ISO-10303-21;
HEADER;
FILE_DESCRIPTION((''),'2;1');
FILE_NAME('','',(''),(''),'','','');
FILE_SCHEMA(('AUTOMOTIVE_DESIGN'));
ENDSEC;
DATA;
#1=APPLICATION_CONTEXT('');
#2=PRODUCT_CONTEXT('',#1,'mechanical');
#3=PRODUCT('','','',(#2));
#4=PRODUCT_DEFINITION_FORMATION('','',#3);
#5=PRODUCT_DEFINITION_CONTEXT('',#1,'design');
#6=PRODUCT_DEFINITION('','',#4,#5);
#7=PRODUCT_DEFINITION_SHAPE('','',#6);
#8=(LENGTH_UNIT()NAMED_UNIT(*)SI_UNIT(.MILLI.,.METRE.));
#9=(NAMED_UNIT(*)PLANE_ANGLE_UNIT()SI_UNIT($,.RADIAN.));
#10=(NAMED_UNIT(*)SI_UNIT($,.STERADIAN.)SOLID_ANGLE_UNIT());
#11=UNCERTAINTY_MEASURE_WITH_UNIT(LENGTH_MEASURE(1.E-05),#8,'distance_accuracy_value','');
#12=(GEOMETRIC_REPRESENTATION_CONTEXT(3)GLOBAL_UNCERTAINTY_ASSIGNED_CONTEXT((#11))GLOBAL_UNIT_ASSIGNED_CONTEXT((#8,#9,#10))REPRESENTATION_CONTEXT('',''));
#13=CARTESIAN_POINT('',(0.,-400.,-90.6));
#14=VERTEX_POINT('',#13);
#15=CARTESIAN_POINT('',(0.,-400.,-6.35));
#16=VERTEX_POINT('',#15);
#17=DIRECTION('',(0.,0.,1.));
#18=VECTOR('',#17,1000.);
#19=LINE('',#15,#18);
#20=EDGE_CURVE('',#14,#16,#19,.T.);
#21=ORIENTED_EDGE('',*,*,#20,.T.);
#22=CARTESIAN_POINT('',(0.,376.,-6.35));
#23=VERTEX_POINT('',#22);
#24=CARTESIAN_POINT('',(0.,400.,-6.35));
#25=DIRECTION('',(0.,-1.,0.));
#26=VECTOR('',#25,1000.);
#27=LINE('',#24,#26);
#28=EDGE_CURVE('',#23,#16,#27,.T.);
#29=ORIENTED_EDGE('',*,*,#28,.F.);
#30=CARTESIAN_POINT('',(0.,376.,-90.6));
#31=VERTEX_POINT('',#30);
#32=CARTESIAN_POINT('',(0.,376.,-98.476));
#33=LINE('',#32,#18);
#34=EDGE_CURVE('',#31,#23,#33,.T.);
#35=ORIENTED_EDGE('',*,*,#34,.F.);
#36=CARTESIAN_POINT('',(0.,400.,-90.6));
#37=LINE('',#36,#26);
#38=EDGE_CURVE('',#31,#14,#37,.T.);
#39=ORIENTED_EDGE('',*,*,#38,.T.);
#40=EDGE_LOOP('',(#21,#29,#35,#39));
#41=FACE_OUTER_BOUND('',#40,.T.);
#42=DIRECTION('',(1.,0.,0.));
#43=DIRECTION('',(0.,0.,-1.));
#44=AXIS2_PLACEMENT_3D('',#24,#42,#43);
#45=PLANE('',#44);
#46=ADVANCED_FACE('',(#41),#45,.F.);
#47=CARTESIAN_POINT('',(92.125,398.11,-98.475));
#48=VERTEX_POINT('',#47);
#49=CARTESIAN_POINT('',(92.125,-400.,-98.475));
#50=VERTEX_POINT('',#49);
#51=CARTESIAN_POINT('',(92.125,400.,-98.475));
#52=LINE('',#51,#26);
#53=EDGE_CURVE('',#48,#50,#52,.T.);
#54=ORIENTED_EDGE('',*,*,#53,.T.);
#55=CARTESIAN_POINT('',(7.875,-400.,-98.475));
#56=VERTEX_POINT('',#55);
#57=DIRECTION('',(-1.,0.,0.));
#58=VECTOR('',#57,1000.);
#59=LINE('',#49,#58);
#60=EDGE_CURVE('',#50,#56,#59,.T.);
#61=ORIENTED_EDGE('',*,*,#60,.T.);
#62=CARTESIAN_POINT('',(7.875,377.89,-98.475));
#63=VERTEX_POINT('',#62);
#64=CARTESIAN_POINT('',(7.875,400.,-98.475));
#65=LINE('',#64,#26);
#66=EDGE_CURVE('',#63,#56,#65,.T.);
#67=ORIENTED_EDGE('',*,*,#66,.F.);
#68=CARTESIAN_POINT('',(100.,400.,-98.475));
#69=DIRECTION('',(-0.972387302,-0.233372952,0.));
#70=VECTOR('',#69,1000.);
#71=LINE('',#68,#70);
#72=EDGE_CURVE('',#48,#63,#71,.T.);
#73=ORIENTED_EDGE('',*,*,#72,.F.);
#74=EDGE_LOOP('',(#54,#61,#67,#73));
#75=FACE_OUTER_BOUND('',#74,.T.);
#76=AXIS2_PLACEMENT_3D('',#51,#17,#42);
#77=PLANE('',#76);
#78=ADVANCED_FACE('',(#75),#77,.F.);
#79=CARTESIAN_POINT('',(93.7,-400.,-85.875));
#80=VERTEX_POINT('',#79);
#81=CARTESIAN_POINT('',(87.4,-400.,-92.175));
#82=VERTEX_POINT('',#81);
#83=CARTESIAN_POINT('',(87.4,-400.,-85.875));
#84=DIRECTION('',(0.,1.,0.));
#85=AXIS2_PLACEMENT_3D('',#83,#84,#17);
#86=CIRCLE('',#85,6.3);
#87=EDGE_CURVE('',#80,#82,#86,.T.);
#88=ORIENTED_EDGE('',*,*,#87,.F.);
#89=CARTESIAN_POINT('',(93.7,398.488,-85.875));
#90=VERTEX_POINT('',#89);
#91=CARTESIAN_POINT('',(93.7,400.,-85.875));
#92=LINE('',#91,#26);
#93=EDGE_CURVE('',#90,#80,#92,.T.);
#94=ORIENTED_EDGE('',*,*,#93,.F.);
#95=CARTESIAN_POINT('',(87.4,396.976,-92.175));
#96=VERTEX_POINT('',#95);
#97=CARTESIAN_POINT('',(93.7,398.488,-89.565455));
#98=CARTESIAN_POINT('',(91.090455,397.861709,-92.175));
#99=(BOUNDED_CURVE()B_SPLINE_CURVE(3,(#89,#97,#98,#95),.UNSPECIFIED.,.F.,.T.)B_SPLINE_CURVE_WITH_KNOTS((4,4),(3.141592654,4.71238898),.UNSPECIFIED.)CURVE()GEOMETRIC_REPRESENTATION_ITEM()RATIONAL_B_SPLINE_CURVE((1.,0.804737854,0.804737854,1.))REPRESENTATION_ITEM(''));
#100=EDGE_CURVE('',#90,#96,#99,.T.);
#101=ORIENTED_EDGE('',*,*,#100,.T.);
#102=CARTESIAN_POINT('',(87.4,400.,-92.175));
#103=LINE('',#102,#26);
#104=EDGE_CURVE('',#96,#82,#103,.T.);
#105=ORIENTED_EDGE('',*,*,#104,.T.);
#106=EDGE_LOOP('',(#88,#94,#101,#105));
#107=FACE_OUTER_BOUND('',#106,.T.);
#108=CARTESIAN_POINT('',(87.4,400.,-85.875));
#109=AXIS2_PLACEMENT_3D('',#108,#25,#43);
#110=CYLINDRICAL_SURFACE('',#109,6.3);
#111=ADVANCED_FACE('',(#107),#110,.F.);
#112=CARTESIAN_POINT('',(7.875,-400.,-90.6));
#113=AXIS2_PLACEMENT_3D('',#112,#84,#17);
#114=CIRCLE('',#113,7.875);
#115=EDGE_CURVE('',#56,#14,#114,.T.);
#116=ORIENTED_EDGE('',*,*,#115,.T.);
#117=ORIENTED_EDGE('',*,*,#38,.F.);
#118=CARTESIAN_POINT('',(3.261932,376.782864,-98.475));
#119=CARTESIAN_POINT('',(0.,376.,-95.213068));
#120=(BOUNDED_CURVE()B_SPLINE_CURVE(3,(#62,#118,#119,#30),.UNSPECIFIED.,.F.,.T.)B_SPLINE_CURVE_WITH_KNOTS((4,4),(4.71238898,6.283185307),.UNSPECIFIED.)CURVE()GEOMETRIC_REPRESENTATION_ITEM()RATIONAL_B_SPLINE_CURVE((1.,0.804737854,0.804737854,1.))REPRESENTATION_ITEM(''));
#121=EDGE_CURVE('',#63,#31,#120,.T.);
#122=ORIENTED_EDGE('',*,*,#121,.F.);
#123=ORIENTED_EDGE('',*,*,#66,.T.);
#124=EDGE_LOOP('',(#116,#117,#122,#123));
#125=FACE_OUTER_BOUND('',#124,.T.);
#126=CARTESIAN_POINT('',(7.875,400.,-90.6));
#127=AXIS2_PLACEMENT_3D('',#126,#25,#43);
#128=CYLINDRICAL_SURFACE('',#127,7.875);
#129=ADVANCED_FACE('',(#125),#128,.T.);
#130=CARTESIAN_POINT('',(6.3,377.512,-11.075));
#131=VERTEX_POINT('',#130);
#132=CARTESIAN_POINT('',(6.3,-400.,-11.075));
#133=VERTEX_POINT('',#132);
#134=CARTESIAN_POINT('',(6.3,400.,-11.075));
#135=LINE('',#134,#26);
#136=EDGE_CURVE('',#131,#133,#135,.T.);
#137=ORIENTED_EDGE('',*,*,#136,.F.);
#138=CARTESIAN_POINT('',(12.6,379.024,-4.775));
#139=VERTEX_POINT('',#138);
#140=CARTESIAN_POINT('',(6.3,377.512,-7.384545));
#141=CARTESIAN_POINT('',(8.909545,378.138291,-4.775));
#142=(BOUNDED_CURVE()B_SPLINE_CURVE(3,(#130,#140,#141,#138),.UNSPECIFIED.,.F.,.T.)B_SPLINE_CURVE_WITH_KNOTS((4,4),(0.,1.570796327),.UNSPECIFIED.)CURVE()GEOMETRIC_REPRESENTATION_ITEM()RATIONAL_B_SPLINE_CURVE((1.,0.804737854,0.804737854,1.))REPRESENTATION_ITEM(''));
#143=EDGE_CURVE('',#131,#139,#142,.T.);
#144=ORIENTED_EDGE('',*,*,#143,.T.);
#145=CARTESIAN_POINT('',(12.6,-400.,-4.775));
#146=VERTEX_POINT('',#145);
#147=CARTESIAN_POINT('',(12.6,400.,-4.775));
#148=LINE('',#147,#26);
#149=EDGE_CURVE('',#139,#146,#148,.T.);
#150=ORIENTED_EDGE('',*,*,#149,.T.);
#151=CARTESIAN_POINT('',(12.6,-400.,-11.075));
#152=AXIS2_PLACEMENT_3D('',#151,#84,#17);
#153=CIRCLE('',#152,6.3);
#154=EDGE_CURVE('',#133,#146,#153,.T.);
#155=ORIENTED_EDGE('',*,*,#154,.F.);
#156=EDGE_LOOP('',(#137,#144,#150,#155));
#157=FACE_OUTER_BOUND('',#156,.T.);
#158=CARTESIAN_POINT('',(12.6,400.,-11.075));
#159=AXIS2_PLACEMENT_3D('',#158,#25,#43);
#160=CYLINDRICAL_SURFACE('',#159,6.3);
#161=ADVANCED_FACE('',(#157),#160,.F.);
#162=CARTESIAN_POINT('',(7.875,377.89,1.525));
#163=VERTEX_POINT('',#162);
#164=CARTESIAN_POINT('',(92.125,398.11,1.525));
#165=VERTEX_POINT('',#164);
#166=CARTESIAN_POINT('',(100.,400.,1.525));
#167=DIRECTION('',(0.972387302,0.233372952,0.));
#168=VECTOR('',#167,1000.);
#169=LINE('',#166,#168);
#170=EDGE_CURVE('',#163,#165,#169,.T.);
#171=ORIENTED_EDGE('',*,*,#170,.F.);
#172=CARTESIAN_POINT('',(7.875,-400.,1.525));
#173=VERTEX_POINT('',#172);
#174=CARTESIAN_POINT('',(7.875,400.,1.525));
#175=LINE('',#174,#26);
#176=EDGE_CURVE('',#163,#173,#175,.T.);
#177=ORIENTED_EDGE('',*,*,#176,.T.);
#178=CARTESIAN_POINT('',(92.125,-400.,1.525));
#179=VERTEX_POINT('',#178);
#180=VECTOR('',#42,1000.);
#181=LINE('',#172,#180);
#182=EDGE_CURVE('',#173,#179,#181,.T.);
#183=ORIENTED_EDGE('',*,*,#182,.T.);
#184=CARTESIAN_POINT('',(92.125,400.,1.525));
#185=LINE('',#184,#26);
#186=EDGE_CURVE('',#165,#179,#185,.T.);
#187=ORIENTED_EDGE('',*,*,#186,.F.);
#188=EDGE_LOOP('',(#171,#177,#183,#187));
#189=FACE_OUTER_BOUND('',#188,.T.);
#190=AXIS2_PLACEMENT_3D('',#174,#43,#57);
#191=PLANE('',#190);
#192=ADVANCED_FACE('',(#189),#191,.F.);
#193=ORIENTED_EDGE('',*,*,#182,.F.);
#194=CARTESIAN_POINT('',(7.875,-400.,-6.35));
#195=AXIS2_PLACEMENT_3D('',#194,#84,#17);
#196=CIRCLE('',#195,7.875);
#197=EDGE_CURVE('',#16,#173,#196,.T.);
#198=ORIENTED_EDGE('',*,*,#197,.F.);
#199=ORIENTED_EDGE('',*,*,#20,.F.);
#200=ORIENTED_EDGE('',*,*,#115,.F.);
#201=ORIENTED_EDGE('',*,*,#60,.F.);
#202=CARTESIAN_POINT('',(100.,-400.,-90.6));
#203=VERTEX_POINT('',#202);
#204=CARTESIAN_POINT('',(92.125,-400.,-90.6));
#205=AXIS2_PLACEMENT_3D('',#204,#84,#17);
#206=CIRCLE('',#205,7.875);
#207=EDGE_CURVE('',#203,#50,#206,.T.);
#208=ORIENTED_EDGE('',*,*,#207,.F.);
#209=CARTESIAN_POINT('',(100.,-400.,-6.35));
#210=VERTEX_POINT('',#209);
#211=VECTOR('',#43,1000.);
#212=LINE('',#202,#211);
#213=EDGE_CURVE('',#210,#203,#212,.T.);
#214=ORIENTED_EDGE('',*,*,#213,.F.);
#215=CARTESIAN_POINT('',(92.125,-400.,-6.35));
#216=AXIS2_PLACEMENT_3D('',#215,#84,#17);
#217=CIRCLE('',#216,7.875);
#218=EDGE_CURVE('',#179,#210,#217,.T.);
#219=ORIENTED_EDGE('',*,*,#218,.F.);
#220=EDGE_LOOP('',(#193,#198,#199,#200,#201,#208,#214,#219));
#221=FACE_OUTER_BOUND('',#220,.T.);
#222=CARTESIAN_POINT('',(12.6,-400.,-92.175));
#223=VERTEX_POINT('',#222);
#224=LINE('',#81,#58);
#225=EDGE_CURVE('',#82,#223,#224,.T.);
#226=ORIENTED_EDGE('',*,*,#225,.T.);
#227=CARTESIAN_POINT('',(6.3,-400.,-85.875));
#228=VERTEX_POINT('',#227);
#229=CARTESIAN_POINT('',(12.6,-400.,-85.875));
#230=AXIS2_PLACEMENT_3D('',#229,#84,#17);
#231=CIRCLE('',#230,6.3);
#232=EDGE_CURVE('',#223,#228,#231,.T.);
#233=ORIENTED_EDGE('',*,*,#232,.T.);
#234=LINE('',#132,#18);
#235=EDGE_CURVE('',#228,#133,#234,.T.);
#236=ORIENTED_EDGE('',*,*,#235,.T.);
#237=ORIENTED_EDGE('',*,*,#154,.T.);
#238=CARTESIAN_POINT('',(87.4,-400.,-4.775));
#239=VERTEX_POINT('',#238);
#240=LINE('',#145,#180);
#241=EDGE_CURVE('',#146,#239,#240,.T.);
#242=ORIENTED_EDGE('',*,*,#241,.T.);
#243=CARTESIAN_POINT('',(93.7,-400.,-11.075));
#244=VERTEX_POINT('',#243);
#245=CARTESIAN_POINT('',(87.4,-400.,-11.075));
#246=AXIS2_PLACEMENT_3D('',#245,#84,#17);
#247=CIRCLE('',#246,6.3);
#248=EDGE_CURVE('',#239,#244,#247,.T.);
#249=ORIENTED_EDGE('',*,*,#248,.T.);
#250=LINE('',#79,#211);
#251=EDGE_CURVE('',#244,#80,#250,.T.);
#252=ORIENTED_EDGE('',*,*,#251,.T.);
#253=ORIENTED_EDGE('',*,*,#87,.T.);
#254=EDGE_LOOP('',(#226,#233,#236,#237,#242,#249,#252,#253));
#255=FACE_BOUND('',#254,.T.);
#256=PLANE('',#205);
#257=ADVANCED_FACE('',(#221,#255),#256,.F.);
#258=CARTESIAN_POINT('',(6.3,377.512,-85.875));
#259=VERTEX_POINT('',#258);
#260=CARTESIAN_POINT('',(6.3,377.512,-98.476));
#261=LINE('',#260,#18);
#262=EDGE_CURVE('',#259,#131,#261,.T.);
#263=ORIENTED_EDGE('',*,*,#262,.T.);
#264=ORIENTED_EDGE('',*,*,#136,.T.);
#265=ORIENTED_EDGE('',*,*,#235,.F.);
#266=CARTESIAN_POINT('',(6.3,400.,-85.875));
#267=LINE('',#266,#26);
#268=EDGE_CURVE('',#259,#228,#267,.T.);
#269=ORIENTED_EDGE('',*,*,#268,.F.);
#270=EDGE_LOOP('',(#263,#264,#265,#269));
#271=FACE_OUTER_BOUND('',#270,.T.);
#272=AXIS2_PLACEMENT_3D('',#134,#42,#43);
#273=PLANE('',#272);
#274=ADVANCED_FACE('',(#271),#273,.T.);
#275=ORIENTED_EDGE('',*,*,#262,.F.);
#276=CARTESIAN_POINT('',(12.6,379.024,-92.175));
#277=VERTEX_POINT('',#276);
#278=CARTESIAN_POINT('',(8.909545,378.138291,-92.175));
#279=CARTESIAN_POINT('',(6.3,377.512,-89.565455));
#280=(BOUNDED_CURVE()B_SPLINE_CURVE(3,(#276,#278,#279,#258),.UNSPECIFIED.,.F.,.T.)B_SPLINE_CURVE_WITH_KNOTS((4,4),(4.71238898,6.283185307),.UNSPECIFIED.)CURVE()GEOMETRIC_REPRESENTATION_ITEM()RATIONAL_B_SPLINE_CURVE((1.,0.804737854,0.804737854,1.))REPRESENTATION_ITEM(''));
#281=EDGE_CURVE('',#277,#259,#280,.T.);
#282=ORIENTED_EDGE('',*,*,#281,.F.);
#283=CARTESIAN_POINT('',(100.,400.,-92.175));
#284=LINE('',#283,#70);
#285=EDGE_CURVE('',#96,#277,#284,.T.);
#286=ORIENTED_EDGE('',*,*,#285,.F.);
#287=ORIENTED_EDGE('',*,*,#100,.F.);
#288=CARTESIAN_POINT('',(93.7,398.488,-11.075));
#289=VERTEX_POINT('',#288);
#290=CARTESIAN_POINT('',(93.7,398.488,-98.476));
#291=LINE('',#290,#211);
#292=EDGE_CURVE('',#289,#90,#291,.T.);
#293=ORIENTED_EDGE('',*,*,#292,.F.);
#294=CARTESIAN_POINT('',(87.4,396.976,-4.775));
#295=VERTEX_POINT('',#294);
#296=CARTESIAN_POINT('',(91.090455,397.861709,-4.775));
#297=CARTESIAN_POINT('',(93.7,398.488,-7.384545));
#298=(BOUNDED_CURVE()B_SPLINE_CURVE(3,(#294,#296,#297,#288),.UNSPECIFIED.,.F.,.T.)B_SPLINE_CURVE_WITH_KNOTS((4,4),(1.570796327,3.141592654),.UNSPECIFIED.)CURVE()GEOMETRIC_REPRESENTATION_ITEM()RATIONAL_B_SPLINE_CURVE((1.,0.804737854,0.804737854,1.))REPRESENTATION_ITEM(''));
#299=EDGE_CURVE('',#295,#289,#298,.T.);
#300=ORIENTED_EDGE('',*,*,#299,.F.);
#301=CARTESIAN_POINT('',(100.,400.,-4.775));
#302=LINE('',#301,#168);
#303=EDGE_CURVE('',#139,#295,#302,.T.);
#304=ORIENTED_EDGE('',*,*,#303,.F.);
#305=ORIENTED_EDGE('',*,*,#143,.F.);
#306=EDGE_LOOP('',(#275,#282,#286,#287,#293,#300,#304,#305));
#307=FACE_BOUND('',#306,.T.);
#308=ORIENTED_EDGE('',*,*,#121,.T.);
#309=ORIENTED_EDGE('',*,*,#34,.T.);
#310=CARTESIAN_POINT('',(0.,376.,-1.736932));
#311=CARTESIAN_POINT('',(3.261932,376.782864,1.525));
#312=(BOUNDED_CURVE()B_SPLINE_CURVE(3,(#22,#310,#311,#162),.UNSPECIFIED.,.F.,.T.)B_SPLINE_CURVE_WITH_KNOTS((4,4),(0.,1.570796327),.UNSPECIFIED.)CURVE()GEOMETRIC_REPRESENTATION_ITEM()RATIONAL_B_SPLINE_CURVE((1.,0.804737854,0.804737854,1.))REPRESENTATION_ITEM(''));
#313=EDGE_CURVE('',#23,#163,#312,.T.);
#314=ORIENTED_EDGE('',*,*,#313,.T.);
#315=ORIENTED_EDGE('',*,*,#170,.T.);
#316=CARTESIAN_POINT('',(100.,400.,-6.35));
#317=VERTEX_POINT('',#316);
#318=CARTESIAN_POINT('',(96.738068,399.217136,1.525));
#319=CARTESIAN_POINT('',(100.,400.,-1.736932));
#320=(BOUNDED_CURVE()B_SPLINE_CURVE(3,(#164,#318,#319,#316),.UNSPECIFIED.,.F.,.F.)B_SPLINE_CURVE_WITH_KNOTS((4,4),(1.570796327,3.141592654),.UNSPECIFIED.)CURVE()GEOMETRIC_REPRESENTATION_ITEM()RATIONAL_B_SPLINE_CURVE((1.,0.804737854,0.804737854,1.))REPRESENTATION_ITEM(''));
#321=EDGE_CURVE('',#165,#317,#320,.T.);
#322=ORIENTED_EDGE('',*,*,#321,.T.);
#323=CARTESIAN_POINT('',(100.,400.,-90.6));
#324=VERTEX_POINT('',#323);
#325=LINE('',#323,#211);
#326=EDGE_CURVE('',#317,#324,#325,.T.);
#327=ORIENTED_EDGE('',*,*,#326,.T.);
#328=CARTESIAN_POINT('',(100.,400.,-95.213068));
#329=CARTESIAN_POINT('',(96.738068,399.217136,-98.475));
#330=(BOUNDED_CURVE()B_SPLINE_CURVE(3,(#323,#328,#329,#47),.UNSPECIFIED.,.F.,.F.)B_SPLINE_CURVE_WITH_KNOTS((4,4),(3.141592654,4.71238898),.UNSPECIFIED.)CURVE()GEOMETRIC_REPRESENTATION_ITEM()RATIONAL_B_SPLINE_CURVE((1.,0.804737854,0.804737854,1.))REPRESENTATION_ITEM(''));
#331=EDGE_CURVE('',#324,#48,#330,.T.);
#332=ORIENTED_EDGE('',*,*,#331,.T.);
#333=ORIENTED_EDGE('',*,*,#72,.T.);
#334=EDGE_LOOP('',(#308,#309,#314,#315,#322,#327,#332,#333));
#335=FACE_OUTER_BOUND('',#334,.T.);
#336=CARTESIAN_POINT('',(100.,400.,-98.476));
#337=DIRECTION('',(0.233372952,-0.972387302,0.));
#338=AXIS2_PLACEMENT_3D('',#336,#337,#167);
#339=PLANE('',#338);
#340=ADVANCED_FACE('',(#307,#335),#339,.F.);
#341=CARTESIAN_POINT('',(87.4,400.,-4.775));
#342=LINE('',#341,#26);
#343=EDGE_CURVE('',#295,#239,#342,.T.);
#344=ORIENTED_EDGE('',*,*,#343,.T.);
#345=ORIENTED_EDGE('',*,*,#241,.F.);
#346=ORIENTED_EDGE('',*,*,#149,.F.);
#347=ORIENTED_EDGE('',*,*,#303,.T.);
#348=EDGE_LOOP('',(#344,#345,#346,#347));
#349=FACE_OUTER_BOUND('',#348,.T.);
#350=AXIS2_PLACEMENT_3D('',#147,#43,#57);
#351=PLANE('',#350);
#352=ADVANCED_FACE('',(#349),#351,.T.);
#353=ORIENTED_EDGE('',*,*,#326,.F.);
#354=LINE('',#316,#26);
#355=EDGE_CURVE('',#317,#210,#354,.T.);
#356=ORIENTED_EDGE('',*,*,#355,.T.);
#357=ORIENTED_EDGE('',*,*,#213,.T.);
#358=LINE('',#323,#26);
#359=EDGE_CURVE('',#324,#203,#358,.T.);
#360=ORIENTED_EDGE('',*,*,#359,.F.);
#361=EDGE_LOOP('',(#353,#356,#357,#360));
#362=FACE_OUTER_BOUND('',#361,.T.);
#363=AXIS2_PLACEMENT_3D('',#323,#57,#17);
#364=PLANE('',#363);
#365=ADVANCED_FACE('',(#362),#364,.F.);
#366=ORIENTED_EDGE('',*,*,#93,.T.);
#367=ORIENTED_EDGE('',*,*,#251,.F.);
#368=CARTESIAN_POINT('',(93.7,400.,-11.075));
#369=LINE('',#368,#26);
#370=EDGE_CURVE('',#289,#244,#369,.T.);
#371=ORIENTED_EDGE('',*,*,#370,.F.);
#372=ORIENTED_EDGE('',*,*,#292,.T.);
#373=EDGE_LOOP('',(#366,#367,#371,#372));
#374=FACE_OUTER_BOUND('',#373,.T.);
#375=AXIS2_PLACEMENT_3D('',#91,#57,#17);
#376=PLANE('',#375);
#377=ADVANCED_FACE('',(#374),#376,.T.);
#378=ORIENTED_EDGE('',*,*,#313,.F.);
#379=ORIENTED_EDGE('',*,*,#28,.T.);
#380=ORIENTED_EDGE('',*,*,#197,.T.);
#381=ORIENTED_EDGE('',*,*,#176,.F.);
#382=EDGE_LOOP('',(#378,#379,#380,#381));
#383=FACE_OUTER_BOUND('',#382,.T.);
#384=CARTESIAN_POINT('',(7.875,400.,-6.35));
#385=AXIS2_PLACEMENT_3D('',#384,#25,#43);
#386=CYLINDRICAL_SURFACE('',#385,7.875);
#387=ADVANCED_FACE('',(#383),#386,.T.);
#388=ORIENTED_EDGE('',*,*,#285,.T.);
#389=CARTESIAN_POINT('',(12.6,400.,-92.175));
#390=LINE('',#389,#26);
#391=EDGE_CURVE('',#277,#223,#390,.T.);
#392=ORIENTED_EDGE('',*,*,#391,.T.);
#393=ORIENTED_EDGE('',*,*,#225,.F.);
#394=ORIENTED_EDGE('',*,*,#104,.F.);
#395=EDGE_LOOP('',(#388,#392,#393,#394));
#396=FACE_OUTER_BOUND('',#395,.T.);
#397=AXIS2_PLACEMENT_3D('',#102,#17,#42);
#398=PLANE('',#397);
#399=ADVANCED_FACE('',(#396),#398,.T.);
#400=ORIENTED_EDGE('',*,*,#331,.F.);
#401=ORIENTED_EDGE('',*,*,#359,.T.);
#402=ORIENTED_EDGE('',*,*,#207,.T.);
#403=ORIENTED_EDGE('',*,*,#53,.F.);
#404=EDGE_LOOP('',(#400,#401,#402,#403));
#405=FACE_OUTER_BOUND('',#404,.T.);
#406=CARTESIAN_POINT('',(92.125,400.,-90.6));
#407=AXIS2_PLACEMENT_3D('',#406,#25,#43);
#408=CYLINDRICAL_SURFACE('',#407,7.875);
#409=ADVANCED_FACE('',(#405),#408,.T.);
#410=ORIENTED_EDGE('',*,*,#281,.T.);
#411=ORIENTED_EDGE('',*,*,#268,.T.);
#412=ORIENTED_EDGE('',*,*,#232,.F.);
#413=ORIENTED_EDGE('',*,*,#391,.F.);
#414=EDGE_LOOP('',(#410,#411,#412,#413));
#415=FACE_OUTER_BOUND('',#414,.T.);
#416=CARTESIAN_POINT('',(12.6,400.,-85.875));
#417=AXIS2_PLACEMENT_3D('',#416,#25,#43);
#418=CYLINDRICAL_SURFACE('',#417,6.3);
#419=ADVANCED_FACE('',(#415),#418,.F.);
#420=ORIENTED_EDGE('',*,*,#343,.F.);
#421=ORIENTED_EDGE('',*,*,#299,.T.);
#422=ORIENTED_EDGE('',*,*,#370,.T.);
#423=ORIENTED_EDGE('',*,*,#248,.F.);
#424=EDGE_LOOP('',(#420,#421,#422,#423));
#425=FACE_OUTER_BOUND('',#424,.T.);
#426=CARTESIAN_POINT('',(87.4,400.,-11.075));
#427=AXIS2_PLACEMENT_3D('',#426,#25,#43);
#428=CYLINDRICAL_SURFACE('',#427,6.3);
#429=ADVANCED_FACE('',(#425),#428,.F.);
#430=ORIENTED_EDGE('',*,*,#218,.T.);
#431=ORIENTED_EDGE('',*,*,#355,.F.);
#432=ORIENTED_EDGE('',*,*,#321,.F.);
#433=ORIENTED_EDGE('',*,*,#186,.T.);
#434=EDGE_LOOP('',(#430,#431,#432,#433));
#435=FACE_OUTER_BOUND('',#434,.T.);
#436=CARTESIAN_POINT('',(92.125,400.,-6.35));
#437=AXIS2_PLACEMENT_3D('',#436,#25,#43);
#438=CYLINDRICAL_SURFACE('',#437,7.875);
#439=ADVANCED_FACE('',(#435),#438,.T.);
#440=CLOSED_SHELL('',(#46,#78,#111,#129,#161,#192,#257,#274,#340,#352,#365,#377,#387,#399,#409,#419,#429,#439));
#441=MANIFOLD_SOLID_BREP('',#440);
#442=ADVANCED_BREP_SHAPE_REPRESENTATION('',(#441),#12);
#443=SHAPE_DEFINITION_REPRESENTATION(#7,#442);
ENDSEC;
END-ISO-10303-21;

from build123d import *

# Parameters (mm, degrees)
BOSS_EXTRUDE1_DEPTH = 400
CUT_EXTRUDE1_REACH  = 426.264


with BuildPart() as part:
    # Sketch2 → Boss-Extrude1 (new, symmetric)
    with BuildSketch(Plane(origin=(0, 0, 0), x_dir=(1, 0, 0), z_dir=(0, 1, 0))):
        with BuildLine():
            Line((7.875, -1.525), (92.125, -1.525))
            ThreePointArc((92.125, -1.525), (97.693465902, 0.781534098), (100, 6.35))
            Line((100, 6.35), (100, 90.6))
            ThreePointArc((100, 90.6), (97.693465902, 96.168465902), (92.125, 98.475))
            Line((92.125, 98.475), (7.875, 98.475))
            ThreePointArc((7.875, 98.475), (2.306534098, 96.168465902), (0, 90.6))
            Line((0, 90.6), (0, 6.35))
            ThreePointArc((0, 6.35), (2.306534098, 0.781534098), (7.875, -1.525))
        make_face()
        with BuildLine():
            Line((12.6, 4.775), (87.4, 4.775))
            ThreePointArc((87.4, 4.775), (91.854772721, 6.620227279), (93.7, 11.075))
            Line((93.7, 11.075), (93.7, 85.875))
            ThreePointArc((93.7, 85.875), (91.854772721, 90.329772721), (87.4, 92.175))
            Line((87.4, 92.175), (12.6, 92.175))
            ThreePointArc((12.6, 92.175), (8.145227279, 90.329772721), (6.3, 85.875))
            Line((6.3, 85.875), (6.3, 11.075))
            ThreePointArc((6.3, 11.075), (8.145227279, 6.620227279), (12.6, 4.775))
        make_face(mode=Mode.SUBTRACT)
    extrude(amount=BOSS_EXTRUDE1_DEPTH, both=True)

    # Sketch4 → Cut-Extrude1 (cut, up to next)
    with BuildSketch(Plane.XY.offset(1.525), mode=Mode.PRIVATE) as cut_extrude1_sk1:
        Polygon((100, 400), (0, 376), (0, 400), align=None)
    cut_extrude1_tool1 = extrude(cut_extrude1_sk1.sketch, amount=-CUT_EXTRUDE1_REACH, mode=Mode.PRIVATE) & part.part
    add(cut_extrude1_tool1.solids().sort_by_distance((33.333333, 392, 1.525))[0], mode=Mode.SUBTRACT)


solid = part.part
